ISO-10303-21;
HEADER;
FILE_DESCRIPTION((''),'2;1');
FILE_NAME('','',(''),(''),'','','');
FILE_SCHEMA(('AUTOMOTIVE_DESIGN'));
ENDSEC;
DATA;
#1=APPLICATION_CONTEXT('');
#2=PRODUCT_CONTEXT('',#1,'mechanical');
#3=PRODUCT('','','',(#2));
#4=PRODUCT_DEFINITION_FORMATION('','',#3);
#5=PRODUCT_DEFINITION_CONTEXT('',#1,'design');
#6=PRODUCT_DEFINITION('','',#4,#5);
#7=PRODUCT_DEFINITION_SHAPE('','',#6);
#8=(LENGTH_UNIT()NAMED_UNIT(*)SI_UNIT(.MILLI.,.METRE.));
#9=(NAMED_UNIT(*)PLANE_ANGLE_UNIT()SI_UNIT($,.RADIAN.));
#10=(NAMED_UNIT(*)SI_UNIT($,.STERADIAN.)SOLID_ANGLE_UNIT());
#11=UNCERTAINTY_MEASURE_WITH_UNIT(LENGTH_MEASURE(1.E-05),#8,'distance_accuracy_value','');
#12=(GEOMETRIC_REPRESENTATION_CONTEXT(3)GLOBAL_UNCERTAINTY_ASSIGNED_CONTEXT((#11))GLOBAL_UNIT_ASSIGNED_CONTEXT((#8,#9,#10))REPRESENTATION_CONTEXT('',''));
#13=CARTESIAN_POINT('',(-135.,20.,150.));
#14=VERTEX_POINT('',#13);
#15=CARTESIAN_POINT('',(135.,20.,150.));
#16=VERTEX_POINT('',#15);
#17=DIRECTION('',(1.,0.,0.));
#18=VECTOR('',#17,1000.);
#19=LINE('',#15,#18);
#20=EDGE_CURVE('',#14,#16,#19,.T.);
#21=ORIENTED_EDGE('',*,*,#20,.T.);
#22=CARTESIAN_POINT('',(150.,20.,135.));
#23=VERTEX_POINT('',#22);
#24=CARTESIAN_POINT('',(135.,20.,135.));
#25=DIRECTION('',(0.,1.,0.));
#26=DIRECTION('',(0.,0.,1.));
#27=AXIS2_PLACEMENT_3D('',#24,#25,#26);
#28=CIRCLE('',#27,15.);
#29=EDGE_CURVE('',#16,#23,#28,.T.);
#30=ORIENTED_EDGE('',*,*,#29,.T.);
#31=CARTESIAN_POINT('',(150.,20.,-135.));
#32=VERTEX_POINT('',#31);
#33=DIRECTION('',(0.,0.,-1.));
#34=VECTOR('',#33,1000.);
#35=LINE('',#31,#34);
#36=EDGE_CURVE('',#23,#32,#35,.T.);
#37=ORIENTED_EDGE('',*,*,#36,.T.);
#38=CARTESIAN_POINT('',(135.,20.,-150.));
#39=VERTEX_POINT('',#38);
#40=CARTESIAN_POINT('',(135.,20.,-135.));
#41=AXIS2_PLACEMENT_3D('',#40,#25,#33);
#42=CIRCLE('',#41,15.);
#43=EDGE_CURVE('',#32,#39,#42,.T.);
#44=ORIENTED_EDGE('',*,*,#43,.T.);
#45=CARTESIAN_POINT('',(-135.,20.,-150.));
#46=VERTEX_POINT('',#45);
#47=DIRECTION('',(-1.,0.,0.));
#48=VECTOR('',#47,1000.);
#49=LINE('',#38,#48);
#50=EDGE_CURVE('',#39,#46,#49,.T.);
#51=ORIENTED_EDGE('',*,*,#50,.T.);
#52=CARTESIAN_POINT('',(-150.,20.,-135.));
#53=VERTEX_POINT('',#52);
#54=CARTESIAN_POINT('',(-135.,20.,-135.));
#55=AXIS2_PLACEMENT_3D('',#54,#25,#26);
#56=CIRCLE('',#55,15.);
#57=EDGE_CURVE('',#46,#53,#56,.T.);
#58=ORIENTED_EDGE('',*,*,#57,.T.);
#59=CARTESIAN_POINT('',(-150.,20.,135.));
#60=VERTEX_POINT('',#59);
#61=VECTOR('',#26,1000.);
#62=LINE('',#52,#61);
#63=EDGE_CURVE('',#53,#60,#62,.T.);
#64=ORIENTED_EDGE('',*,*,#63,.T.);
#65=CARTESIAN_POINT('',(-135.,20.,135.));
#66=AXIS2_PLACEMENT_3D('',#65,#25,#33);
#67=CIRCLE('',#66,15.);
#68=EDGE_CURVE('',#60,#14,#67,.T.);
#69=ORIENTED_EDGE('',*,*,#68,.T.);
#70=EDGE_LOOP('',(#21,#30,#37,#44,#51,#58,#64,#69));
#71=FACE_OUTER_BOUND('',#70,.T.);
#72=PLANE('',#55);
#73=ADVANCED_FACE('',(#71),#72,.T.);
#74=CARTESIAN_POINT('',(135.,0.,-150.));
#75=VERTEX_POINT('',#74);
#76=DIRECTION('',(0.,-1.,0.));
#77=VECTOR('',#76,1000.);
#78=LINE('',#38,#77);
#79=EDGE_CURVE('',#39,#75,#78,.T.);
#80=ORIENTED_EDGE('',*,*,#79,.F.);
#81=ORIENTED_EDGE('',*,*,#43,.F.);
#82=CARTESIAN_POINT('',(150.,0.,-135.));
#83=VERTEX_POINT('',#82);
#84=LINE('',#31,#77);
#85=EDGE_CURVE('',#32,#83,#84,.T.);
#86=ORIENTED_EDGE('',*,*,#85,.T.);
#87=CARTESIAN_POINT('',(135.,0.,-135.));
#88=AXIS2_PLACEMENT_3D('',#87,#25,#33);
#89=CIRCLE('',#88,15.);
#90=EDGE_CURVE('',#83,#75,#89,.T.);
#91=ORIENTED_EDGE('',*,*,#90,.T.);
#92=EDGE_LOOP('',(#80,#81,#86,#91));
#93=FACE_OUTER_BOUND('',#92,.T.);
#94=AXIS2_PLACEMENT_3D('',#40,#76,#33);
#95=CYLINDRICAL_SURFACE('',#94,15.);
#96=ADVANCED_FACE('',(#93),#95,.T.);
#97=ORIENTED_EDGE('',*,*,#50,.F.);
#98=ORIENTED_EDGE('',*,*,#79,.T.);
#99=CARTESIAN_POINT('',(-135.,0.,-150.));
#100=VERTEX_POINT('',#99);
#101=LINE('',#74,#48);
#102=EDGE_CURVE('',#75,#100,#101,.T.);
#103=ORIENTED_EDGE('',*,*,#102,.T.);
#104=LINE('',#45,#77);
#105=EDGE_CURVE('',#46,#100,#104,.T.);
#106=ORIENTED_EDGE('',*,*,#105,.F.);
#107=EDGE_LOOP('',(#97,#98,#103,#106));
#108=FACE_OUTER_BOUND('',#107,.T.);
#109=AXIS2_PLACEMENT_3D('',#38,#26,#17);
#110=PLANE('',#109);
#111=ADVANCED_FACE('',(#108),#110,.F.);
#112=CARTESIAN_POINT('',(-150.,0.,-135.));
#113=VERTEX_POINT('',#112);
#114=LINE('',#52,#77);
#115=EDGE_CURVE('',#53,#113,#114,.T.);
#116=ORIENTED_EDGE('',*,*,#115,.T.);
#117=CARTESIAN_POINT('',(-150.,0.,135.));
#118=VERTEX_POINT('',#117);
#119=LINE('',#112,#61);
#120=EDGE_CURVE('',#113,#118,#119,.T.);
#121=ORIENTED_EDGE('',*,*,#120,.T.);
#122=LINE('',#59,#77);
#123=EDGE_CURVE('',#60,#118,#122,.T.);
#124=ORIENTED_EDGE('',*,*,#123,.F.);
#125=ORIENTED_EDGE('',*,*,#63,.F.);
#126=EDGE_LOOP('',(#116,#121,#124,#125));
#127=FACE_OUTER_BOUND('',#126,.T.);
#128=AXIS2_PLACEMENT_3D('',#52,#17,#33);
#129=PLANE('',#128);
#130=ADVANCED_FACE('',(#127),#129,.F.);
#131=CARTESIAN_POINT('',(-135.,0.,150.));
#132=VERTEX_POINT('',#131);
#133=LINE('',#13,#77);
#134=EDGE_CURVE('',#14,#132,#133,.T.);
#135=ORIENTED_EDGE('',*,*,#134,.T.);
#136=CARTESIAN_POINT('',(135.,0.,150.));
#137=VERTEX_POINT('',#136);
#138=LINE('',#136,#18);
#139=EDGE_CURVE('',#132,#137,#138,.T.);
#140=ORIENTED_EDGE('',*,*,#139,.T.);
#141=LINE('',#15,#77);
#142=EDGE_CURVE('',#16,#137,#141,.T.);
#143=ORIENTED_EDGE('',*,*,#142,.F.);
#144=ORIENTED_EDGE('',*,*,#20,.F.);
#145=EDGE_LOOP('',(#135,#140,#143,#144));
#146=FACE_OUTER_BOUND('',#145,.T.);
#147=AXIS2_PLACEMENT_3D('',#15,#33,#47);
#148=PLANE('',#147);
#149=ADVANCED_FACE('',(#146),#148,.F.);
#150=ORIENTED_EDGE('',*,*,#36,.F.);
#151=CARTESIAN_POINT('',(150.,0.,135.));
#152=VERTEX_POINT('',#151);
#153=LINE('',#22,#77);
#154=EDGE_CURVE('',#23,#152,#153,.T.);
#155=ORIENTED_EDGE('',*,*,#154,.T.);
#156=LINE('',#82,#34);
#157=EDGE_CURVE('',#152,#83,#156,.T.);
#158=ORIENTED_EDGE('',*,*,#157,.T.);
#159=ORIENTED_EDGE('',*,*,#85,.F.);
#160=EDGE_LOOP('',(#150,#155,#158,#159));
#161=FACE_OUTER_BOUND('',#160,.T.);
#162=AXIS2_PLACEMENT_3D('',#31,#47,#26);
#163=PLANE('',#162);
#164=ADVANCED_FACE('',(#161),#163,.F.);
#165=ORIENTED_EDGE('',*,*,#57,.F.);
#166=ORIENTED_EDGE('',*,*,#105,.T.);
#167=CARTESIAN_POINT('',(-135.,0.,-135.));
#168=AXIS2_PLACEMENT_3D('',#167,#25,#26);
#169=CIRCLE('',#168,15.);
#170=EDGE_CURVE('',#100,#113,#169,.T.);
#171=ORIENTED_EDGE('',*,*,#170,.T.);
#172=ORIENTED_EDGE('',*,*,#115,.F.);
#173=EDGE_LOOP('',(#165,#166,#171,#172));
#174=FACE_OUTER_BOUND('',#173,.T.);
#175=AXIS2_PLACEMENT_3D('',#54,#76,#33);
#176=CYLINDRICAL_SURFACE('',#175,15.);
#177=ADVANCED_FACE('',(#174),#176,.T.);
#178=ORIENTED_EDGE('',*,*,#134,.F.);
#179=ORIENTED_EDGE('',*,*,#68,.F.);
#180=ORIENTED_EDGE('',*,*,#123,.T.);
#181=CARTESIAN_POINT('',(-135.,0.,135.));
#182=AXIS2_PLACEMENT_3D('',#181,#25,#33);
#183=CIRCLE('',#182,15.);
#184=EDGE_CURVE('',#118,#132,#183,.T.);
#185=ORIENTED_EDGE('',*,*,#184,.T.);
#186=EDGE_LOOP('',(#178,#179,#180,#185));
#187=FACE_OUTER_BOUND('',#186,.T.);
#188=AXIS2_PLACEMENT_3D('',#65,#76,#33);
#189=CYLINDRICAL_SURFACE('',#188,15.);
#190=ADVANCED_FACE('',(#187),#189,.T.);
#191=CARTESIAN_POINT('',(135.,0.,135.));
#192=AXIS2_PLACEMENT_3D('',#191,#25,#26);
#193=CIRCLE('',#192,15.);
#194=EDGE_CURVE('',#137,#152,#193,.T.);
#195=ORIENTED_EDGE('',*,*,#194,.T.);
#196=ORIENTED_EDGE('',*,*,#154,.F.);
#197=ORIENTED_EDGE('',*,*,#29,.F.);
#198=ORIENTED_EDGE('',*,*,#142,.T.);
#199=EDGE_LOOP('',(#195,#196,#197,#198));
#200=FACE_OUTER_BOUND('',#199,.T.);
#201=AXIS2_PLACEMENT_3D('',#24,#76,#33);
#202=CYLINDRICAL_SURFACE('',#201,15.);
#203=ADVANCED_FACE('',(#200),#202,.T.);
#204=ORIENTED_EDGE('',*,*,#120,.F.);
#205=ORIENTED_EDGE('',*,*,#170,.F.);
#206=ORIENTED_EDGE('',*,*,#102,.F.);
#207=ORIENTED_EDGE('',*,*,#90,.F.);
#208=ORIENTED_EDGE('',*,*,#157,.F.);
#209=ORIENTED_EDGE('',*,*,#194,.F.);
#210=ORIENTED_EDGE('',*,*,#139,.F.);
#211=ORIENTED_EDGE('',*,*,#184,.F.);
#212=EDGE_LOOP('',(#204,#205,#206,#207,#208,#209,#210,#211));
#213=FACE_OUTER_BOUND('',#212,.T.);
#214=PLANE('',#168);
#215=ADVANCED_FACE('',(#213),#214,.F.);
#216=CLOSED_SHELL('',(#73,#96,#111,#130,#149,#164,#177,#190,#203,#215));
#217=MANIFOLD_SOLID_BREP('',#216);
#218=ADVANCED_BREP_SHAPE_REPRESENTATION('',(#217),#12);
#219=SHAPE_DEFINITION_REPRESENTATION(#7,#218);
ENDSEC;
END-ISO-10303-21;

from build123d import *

# Parameters (mm, degrees)
BOSS_EXTRUDE_1_DEPTH = 20


with BuildPart() as part:
    # Sketch 1 → Boss-Extrude 1 (new body)
    with BuildSketch(Plane(origin=(0, 0, 0), x_dir=(1, 0, 0), z_dir=(0, 1, 0))):
        with BuildLine():
            Line((135, 150), (-135, 150))
            ThreePointArc((-135, 150), (-145.606601718, 145.606601718), (-150, 135))
            Line((-150, 135), (-150, -135))
            ThreePointArc((-150, -135), (-145.606601718, -145.606601718), (-135, -150))
            Line((-135, -150), (135, -150))
            ThreePointArc((135, -150), (145.606601718, -145.606601718), (150, -135))
            Line((150, -135), (150, 135))
            ThreePointArc((150, 135), (145.606601718, 145.606601718), (135, 150))
        make_face()
    extrude(amount=BOSS_EXTRUDE_1_DEPTH)


solid = part.part
